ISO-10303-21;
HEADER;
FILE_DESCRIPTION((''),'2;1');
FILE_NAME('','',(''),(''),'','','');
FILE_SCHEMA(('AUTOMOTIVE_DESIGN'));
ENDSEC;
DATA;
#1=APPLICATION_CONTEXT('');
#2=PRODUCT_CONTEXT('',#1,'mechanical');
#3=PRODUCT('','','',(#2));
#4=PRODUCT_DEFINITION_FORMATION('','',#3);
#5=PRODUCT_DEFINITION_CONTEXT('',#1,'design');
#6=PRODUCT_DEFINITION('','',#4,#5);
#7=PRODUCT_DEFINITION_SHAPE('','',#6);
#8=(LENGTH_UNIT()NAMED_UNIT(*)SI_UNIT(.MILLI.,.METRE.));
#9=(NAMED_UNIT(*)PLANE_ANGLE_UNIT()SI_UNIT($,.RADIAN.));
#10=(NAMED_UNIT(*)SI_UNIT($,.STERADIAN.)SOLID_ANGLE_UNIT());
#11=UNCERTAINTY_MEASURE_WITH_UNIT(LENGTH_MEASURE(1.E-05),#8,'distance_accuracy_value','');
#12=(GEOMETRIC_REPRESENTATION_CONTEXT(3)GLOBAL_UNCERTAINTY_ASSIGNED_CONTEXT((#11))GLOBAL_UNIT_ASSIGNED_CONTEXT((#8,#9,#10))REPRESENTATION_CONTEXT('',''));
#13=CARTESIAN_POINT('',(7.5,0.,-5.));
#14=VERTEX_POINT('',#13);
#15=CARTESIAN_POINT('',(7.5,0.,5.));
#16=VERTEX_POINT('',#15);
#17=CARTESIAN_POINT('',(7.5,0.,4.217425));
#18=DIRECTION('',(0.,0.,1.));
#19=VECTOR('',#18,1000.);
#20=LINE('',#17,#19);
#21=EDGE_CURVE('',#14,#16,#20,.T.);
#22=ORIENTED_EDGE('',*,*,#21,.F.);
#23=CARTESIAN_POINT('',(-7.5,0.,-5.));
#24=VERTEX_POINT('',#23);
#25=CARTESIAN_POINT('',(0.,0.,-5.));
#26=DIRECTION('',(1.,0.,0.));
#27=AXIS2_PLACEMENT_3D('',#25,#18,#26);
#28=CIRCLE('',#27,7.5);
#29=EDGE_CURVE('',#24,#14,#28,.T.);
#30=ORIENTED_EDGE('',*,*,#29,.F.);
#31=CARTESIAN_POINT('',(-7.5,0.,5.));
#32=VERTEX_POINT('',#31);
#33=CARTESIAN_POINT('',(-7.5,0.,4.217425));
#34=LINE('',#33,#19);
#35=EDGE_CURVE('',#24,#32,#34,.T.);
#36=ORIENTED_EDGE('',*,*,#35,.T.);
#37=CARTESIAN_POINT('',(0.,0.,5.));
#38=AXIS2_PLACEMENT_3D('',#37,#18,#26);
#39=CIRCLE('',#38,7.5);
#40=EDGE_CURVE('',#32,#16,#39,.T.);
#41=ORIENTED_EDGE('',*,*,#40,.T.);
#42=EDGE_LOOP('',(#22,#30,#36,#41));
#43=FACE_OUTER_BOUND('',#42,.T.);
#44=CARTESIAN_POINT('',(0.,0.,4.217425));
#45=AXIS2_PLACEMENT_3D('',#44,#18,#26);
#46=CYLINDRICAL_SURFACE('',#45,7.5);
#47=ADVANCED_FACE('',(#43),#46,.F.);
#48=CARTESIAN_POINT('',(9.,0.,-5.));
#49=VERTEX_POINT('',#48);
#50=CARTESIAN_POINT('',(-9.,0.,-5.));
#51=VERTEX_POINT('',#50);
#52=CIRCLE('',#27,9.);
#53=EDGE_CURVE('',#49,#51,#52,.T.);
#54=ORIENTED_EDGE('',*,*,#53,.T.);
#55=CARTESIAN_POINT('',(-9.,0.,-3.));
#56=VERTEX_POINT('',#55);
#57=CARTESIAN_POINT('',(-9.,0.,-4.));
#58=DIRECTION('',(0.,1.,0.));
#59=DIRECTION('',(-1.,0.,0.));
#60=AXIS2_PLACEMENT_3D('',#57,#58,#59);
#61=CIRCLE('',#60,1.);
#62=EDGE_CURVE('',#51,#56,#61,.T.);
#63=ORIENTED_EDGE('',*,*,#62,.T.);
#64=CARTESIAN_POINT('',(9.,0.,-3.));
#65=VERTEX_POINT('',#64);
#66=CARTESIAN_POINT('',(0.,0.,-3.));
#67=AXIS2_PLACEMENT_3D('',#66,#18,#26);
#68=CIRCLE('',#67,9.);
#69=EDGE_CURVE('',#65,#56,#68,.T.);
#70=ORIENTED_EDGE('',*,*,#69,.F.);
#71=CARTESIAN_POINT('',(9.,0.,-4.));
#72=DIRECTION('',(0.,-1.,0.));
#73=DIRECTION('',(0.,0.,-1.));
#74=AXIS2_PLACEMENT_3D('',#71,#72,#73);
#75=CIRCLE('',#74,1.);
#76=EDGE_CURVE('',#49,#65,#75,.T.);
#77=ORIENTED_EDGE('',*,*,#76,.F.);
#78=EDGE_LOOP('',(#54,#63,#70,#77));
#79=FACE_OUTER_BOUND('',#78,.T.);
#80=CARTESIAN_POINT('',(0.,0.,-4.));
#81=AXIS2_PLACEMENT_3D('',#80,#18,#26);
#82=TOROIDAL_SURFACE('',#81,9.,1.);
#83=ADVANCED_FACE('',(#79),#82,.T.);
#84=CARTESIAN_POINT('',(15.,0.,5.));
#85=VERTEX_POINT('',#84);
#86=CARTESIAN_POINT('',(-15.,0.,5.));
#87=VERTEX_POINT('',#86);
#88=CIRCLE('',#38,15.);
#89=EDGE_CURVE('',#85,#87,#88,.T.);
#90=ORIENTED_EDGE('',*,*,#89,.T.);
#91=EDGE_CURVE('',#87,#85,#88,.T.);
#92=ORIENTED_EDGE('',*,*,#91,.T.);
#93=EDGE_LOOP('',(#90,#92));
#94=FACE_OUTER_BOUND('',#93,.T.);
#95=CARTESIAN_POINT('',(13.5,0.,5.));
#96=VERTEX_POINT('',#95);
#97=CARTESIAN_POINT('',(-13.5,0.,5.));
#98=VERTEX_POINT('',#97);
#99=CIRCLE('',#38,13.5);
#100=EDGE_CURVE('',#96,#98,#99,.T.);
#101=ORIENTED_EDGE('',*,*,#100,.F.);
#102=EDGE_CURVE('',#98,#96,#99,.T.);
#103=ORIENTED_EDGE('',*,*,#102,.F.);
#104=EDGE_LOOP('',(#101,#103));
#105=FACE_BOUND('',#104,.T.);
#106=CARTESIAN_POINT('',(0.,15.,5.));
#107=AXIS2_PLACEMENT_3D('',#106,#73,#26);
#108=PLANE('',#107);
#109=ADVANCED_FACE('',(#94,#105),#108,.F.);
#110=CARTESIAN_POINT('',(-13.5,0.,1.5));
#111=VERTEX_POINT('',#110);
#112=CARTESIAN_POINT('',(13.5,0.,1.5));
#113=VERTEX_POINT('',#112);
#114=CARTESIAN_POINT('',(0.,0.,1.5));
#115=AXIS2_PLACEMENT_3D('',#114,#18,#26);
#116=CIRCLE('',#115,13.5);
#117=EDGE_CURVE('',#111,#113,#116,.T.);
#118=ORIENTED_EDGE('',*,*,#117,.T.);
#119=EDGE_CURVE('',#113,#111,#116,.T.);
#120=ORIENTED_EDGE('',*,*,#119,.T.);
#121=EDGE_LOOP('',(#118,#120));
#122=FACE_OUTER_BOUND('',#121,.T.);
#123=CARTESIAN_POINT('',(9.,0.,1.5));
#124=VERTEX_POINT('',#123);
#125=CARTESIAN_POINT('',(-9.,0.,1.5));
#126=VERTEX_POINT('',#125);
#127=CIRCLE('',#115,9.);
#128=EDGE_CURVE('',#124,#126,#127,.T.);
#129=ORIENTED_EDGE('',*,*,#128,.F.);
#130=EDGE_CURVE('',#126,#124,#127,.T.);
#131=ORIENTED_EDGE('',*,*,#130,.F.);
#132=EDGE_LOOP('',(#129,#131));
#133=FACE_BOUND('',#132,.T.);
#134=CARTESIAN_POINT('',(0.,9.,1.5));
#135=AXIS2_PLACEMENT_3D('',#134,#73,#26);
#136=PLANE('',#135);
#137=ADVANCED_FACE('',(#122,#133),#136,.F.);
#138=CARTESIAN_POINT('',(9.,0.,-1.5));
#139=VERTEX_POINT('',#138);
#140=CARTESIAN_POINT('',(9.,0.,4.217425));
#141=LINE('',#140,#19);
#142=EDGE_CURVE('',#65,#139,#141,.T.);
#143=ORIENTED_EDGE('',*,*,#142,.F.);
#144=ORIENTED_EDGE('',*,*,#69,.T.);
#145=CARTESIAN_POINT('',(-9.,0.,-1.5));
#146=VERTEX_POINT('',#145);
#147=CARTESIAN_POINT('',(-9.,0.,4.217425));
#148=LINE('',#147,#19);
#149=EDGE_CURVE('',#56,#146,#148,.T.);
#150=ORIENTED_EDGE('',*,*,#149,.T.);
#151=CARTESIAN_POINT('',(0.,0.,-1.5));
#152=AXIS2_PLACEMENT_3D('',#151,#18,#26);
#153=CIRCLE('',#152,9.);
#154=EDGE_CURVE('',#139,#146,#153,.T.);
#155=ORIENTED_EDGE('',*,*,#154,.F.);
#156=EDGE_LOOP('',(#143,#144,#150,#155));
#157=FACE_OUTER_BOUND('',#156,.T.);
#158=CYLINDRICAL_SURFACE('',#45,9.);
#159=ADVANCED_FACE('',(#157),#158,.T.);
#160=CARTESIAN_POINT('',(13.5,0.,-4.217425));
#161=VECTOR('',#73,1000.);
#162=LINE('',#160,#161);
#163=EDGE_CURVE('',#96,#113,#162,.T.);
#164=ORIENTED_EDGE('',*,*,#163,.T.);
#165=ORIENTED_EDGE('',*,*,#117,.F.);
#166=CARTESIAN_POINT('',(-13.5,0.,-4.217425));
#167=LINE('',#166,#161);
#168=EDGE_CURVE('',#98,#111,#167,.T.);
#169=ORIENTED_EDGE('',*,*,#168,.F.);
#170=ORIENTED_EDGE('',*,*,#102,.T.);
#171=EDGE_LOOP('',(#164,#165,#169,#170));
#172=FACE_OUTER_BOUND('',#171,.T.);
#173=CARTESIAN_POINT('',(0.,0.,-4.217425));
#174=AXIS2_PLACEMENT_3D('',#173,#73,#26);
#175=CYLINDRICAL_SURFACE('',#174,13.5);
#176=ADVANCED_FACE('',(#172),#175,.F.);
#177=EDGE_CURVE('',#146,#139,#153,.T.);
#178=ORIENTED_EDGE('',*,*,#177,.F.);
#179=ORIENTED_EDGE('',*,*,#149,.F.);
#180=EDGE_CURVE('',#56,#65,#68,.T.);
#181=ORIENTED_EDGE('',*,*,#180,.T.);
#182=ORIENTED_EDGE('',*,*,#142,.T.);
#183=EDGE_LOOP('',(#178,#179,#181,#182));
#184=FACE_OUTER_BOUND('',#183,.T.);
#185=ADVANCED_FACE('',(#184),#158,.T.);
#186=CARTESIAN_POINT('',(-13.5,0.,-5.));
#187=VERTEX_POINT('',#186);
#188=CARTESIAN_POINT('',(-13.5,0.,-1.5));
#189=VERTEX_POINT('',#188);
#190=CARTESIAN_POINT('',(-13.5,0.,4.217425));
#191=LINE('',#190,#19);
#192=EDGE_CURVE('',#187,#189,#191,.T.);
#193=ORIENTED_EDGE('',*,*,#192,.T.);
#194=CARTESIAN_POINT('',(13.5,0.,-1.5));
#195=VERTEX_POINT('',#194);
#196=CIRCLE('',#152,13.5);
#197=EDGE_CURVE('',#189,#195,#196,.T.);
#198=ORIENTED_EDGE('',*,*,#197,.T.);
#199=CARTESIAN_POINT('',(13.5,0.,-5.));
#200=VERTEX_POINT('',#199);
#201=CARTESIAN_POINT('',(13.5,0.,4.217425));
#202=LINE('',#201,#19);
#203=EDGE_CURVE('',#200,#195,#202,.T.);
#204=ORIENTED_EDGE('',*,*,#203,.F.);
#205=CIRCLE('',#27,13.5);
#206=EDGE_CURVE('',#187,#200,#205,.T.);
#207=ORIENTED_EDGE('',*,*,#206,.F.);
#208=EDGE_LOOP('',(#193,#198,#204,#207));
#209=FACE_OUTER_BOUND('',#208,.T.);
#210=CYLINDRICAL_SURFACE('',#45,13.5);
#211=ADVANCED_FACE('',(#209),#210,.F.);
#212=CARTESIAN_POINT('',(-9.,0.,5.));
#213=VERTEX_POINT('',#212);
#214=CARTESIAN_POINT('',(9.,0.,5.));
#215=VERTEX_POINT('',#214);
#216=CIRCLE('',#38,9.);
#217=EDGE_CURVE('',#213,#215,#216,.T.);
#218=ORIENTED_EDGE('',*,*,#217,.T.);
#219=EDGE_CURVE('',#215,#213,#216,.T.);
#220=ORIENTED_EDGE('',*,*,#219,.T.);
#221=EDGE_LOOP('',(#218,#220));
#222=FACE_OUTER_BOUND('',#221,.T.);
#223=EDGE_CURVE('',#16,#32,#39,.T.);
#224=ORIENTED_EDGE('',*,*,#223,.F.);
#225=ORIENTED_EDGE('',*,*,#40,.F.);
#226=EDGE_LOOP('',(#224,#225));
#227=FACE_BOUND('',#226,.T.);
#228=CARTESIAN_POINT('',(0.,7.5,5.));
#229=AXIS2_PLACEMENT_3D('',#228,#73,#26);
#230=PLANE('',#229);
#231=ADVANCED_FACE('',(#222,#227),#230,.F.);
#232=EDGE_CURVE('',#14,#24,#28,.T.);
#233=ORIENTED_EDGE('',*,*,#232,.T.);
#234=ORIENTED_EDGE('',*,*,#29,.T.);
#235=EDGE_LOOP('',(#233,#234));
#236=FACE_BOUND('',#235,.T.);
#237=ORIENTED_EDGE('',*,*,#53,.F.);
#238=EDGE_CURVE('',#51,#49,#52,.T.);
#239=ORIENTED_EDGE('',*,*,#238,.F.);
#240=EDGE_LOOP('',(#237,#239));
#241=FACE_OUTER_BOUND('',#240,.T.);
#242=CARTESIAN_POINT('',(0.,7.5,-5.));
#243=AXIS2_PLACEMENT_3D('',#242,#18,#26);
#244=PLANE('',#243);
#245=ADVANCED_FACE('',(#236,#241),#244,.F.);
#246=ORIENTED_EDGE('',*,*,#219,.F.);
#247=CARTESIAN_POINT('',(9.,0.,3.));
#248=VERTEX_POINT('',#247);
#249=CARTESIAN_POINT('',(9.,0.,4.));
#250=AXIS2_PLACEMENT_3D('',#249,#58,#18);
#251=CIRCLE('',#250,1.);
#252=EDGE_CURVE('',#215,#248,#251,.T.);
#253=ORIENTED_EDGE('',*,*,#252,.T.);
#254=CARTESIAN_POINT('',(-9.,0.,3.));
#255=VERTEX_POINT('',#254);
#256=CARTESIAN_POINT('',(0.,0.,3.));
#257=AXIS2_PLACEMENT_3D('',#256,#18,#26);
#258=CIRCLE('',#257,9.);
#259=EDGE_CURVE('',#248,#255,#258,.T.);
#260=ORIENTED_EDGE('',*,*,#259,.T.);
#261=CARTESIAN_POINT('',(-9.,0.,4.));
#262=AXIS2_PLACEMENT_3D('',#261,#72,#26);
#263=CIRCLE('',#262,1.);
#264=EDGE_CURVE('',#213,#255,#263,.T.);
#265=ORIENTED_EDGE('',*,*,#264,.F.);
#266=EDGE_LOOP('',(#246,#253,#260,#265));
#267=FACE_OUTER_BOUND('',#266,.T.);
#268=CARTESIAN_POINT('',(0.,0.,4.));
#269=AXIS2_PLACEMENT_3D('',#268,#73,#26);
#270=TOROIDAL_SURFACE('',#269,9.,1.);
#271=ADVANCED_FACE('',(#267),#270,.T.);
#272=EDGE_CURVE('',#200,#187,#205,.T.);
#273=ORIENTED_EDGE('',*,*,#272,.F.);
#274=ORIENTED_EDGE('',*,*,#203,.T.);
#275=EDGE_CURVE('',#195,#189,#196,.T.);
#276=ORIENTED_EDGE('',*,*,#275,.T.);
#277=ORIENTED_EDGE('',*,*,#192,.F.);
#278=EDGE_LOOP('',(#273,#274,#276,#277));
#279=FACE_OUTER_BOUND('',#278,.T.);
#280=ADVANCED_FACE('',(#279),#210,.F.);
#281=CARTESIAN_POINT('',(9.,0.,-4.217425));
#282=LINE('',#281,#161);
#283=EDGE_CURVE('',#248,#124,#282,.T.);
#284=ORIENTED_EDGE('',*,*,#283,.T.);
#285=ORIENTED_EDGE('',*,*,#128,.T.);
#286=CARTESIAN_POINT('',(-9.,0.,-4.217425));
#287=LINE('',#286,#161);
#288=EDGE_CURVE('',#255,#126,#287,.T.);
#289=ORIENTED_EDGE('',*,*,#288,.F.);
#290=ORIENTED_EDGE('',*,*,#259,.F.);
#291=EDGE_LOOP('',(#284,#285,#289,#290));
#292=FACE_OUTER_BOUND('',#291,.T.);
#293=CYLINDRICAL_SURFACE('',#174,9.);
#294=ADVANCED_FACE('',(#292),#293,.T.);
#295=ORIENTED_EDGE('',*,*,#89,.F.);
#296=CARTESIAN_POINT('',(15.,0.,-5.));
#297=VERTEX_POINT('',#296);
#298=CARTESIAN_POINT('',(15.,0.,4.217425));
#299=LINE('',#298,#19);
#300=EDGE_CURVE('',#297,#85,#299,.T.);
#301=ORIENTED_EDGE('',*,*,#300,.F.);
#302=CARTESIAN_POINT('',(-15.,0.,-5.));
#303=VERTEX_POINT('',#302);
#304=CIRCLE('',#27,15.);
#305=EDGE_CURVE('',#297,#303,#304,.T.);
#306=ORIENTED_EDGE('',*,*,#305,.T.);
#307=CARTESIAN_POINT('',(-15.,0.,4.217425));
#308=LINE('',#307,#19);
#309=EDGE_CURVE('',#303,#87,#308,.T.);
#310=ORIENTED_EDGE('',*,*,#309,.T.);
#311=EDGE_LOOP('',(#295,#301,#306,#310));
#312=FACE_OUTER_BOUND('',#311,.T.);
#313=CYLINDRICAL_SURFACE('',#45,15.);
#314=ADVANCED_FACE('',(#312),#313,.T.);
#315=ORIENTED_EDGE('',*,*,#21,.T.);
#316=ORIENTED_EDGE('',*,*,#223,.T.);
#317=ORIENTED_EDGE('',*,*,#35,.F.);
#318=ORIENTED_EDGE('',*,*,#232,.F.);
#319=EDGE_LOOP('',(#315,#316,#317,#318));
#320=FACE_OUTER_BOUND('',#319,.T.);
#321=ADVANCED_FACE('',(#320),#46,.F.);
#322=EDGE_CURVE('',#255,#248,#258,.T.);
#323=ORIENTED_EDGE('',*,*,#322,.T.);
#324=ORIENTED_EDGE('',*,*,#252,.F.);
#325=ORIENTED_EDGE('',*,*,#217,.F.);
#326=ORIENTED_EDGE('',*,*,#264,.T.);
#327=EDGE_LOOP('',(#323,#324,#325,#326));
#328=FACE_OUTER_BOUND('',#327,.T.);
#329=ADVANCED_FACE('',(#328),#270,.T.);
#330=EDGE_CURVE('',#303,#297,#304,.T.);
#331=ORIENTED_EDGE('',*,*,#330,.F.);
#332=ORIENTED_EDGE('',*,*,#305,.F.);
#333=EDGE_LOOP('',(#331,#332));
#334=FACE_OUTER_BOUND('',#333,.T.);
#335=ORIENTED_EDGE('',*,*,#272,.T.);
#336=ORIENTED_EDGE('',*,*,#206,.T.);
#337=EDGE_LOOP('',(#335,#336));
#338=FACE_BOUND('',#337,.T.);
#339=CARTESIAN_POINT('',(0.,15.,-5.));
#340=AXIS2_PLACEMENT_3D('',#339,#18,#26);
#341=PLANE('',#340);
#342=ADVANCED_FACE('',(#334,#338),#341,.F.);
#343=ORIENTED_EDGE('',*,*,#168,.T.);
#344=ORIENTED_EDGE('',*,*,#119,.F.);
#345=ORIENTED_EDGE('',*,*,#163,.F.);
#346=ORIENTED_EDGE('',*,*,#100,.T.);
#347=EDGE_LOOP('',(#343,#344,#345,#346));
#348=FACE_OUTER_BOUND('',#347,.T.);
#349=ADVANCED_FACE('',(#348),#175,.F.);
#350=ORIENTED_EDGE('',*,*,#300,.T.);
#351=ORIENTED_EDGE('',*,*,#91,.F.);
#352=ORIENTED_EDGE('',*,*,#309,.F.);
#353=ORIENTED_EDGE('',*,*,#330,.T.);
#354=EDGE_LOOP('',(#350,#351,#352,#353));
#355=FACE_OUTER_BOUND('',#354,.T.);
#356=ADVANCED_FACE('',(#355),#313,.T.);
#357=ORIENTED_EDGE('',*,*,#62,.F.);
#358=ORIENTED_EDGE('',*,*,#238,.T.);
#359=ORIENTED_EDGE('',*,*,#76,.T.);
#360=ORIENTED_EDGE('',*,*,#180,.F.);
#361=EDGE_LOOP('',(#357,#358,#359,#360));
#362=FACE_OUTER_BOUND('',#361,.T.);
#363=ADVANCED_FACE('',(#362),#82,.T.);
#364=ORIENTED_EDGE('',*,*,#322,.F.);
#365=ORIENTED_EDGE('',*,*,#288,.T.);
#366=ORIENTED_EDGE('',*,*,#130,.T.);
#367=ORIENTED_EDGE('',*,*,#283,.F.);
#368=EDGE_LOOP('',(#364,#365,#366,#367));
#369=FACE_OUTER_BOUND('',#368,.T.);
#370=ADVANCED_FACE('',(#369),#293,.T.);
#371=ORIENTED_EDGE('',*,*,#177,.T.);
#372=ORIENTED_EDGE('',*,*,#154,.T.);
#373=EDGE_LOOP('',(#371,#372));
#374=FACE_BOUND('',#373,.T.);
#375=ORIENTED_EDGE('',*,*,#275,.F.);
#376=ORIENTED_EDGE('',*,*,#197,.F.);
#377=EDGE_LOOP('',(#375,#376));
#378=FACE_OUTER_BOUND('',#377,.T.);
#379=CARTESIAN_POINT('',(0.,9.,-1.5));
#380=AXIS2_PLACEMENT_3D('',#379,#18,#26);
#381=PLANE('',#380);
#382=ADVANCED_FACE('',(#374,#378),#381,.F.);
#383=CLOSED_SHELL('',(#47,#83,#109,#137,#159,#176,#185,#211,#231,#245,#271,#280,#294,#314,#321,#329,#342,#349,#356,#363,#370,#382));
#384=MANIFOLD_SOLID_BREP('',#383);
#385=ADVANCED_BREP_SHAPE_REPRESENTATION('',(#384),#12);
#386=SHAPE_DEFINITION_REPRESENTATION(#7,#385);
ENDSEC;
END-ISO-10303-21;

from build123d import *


with BuildPart() as part:
    # 草图1 → 旋转2 (revolve)
    with BuildSketch(Plane(origin=(0, 0, 0), x_dir=(0, 0, -1), z_dir=(1, 0, 0)), mode=Mode.PRIVATE) as revolve_2_sk:
        with BuildLine():
            Line((0, 15), (0, 7.5))
            Line((0, 7.5), (5, 7.5))
            Line((5, 7.5), (5, 9))
            ThreePointArc((5, 9), (4, 10), (3, 9))
            Line((3, 9), (1.5, 9))
            Line((1.5, 9), (1.5, 13.5))
            Line((1.5, 13.5), (5, 13.5))
            Line((5, 13.5), (5, 15))
            Line((5, 15), (0, 15))
        make_face()
    revolve_2 = revolve(revolve_2_sk.sketch.rotate(Axis((0, 0, 4.217424625), (0, 0, -1)), 90), axis=Axis((0, 0, 4.217424625), (0, 0, -1)))

    # 镜向2: 旋转2 across plane
    add(revolve_2.mirror(Plane(origin=(0, 15, 0), x_dir=(1, 0, 0), z_dir=(0, 0, -1))))


solid = part.part
